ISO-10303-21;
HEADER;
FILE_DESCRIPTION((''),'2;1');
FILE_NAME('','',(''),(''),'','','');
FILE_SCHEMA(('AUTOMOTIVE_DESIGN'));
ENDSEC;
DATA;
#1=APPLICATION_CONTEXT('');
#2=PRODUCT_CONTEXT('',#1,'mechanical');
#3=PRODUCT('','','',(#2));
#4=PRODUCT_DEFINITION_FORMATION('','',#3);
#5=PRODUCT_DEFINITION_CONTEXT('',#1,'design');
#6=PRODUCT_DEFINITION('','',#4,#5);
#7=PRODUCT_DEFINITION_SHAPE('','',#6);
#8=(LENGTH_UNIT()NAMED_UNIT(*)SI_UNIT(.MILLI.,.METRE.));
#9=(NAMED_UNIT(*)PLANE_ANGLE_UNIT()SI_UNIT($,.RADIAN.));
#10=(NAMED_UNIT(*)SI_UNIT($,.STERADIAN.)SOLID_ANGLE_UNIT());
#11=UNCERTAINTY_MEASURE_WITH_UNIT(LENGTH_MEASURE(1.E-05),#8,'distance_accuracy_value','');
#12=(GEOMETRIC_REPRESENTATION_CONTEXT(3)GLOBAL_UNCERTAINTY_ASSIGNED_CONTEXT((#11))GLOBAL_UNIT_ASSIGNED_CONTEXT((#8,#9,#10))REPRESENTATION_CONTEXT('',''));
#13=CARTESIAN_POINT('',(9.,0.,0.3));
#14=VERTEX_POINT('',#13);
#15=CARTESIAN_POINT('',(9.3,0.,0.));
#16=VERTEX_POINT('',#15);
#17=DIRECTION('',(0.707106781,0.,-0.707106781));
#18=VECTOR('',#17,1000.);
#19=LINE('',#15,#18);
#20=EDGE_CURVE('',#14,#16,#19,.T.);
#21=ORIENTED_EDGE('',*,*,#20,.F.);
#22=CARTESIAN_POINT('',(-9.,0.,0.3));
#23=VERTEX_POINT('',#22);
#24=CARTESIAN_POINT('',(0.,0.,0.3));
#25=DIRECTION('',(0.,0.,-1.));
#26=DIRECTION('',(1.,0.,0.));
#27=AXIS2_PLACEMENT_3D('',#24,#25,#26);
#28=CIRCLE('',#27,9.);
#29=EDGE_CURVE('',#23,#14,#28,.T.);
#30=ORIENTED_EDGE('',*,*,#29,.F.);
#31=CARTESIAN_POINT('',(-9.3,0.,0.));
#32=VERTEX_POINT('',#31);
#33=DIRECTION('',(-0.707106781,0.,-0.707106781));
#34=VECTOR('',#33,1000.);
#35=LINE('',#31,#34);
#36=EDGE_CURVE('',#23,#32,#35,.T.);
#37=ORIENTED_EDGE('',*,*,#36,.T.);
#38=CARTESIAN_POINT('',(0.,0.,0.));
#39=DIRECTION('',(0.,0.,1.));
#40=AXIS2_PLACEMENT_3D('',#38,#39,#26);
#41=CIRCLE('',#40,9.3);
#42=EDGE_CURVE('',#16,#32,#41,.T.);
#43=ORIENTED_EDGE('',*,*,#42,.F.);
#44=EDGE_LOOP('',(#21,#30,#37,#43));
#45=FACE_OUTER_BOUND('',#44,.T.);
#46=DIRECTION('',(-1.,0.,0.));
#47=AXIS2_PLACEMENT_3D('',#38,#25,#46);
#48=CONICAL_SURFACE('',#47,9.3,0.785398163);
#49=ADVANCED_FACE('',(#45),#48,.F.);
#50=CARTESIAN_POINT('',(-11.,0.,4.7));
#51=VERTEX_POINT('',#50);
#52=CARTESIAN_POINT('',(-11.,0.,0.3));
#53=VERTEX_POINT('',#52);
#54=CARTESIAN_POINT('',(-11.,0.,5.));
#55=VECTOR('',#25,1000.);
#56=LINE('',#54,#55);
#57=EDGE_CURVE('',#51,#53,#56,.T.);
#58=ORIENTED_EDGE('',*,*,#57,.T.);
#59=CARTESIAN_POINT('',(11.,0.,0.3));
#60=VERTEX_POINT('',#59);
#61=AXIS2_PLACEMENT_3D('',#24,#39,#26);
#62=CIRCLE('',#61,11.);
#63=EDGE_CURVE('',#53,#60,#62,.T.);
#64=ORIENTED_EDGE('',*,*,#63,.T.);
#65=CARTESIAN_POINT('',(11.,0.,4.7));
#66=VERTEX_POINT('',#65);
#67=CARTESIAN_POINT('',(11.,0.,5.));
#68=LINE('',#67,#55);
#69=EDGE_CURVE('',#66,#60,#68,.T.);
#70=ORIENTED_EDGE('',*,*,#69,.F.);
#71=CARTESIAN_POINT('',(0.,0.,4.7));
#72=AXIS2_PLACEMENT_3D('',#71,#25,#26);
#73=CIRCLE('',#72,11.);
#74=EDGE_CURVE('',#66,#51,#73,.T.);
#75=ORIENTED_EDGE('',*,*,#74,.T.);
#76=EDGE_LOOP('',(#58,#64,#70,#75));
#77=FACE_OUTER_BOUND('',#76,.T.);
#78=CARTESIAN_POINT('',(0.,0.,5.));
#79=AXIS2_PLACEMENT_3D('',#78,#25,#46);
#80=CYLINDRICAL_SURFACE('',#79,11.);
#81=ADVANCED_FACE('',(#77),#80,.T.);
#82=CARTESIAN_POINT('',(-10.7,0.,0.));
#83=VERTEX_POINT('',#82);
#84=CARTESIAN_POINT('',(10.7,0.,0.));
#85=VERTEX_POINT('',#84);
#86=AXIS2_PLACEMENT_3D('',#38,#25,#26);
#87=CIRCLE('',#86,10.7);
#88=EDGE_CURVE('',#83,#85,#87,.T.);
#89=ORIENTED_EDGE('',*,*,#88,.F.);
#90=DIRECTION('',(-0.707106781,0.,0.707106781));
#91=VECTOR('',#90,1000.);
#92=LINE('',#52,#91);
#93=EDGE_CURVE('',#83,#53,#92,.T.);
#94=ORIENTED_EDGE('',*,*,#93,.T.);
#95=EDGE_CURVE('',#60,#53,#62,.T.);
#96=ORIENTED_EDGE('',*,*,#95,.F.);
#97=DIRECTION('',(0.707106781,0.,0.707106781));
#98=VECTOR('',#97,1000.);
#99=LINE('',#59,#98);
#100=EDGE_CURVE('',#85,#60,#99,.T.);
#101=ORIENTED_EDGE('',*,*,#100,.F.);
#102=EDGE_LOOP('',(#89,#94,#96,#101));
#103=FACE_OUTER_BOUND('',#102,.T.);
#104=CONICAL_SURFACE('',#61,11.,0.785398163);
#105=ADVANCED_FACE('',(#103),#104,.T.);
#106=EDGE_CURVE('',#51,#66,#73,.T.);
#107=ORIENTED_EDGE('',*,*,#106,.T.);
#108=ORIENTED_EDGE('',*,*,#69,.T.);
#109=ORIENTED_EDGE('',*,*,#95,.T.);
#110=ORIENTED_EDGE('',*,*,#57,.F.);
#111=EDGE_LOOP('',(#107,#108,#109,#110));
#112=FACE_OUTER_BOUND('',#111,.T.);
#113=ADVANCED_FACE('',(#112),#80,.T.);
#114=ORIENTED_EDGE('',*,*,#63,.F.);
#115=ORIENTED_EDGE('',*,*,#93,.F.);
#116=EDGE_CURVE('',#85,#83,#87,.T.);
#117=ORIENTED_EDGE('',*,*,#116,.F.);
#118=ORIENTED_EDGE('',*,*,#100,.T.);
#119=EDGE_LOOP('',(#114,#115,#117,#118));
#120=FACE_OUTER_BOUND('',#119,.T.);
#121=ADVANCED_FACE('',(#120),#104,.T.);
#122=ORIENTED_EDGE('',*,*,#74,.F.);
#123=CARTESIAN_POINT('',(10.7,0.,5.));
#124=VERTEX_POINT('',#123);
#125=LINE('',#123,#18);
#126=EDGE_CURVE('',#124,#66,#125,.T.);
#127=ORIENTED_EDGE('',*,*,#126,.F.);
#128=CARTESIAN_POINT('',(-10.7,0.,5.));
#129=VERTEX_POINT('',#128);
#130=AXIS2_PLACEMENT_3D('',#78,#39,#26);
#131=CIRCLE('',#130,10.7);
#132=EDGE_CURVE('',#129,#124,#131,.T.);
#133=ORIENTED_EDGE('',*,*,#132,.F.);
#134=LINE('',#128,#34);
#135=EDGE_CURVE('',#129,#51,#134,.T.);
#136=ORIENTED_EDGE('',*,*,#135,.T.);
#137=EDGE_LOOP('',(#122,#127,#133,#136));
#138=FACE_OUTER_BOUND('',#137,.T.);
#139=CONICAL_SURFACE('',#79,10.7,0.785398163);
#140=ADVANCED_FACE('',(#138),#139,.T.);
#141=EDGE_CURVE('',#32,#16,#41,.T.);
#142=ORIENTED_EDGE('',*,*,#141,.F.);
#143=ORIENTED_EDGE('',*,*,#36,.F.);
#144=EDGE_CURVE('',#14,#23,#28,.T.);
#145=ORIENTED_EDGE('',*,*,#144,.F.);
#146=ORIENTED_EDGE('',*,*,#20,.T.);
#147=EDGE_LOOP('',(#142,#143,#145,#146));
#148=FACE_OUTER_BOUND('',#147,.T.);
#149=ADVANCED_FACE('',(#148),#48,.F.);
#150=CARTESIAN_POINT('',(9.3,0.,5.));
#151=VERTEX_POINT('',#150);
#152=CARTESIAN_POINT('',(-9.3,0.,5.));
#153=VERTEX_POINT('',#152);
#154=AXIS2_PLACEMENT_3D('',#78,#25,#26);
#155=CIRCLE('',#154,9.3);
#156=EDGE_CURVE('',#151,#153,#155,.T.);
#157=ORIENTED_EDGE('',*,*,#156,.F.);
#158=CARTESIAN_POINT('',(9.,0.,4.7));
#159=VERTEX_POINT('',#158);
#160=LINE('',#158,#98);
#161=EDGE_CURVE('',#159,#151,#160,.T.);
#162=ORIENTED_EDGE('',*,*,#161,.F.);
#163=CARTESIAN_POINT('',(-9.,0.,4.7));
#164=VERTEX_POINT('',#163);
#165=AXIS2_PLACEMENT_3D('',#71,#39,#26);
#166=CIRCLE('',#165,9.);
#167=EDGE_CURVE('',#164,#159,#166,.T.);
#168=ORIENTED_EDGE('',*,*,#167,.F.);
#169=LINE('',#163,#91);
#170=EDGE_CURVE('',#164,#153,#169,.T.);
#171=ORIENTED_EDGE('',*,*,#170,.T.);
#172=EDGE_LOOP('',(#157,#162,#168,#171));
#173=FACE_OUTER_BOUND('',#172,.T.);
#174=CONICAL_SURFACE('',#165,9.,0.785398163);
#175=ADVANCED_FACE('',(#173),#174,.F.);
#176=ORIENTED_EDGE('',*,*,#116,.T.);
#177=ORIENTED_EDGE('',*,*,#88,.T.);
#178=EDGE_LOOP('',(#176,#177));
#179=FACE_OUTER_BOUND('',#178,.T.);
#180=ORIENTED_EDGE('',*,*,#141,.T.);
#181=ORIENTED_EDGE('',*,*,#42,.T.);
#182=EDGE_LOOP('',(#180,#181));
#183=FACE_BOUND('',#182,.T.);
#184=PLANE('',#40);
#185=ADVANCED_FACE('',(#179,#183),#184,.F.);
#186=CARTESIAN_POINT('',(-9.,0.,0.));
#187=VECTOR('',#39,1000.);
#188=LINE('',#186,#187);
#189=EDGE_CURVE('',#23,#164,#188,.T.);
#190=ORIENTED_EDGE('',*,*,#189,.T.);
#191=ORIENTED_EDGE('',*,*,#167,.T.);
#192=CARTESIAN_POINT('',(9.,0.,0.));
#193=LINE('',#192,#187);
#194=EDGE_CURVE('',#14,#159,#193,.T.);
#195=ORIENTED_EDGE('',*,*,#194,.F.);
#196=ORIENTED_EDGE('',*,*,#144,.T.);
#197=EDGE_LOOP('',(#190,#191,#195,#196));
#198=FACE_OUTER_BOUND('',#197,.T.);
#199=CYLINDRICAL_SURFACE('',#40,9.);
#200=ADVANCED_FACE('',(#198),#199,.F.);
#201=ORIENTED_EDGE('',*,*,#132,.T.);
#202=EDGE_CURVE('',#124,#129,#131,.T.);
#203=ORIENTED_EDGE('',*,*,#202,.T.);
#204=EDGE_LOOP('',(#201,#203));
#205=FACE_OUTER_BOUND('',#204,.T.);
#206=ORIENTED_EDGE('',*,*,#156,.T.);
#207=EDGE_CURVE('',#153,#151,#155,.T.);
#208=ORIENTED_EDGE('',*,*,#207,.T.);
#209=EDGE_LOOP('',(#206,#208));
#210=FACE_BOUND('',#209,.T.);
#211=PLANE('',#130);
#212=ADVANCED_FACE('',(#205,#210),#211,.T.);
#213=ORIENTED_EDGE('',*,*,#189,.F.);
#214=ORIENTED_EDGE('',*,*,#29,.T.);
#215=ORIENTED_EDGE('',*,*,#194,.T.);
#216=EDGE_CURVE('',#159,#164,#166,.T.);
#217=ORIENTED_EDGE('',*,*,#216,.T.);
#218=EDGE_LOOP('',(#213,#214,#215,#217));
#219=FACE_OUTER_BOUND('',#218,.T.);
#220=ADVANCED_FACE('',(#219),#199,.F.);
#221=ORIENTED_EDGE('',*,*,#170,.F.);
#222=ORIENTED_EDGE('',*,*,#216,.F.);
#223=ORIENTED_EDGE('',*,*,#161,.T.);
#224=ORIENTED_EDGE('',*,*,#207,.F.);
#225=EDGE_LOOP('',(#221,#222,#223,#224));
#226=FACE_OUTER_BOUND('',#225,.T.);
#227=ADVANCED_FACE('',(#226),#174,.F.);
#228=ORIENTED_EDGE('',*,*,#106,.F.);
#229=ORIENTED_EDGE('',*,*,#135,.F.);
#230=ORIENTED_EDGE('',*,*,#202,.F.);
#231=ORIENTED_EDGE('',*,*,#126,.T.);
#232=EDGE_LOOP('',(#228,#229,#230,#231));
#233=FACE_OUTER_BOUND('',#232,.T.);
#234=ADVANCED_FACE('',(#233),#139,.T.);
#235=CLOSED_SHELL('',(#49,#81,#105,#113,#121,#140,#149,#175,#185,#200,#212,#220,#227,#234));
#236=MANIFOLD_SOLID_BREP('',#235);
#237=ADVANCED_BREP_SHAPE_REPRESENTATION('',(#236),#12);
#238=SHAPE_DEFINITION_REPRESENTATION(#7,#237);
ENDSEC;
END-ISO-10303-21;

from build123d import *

# Parameters (mm, degrees)
SKETCH_2_R          = 11
EXTRUDE_1_DEPTH     = 5
SKETCH_3_R          = 9
CUT_EXTRUDE_1_DEPTH = 5
CHAMFER_2_SIZE      = 0.3


with BuildPart() as part:
    # 草图2 → 凸台-拉伸1 (new body)
    with BuildSketch(Plane.XY):
        Circle(SKETCH_2_R)
    extrude(amount=EXTRUDE_1_DEPTH)

    # 草图3 → 切除-拉伸1 (cut)
    with BuildSketch(Plane.XY.offset(5)):
        Circle(SKETCH_3_R)
    extrude(amount=-CUT_EXTRUDE_1_DEPTH, mode=Mode.SUBTRACT)

    # 倒角2
    chamfer_2_edges = [part.edges().sort_by_distance(p)[0] for p in [
        (-11, 0, 0),
        (-11, 0, 5),
        (-9, 0, 0),
        (-9, 0, 5),
    ]]
    chamfer(chamfer_2_edges, length=CHAMFER_2_SIZE)


solid = part.part
